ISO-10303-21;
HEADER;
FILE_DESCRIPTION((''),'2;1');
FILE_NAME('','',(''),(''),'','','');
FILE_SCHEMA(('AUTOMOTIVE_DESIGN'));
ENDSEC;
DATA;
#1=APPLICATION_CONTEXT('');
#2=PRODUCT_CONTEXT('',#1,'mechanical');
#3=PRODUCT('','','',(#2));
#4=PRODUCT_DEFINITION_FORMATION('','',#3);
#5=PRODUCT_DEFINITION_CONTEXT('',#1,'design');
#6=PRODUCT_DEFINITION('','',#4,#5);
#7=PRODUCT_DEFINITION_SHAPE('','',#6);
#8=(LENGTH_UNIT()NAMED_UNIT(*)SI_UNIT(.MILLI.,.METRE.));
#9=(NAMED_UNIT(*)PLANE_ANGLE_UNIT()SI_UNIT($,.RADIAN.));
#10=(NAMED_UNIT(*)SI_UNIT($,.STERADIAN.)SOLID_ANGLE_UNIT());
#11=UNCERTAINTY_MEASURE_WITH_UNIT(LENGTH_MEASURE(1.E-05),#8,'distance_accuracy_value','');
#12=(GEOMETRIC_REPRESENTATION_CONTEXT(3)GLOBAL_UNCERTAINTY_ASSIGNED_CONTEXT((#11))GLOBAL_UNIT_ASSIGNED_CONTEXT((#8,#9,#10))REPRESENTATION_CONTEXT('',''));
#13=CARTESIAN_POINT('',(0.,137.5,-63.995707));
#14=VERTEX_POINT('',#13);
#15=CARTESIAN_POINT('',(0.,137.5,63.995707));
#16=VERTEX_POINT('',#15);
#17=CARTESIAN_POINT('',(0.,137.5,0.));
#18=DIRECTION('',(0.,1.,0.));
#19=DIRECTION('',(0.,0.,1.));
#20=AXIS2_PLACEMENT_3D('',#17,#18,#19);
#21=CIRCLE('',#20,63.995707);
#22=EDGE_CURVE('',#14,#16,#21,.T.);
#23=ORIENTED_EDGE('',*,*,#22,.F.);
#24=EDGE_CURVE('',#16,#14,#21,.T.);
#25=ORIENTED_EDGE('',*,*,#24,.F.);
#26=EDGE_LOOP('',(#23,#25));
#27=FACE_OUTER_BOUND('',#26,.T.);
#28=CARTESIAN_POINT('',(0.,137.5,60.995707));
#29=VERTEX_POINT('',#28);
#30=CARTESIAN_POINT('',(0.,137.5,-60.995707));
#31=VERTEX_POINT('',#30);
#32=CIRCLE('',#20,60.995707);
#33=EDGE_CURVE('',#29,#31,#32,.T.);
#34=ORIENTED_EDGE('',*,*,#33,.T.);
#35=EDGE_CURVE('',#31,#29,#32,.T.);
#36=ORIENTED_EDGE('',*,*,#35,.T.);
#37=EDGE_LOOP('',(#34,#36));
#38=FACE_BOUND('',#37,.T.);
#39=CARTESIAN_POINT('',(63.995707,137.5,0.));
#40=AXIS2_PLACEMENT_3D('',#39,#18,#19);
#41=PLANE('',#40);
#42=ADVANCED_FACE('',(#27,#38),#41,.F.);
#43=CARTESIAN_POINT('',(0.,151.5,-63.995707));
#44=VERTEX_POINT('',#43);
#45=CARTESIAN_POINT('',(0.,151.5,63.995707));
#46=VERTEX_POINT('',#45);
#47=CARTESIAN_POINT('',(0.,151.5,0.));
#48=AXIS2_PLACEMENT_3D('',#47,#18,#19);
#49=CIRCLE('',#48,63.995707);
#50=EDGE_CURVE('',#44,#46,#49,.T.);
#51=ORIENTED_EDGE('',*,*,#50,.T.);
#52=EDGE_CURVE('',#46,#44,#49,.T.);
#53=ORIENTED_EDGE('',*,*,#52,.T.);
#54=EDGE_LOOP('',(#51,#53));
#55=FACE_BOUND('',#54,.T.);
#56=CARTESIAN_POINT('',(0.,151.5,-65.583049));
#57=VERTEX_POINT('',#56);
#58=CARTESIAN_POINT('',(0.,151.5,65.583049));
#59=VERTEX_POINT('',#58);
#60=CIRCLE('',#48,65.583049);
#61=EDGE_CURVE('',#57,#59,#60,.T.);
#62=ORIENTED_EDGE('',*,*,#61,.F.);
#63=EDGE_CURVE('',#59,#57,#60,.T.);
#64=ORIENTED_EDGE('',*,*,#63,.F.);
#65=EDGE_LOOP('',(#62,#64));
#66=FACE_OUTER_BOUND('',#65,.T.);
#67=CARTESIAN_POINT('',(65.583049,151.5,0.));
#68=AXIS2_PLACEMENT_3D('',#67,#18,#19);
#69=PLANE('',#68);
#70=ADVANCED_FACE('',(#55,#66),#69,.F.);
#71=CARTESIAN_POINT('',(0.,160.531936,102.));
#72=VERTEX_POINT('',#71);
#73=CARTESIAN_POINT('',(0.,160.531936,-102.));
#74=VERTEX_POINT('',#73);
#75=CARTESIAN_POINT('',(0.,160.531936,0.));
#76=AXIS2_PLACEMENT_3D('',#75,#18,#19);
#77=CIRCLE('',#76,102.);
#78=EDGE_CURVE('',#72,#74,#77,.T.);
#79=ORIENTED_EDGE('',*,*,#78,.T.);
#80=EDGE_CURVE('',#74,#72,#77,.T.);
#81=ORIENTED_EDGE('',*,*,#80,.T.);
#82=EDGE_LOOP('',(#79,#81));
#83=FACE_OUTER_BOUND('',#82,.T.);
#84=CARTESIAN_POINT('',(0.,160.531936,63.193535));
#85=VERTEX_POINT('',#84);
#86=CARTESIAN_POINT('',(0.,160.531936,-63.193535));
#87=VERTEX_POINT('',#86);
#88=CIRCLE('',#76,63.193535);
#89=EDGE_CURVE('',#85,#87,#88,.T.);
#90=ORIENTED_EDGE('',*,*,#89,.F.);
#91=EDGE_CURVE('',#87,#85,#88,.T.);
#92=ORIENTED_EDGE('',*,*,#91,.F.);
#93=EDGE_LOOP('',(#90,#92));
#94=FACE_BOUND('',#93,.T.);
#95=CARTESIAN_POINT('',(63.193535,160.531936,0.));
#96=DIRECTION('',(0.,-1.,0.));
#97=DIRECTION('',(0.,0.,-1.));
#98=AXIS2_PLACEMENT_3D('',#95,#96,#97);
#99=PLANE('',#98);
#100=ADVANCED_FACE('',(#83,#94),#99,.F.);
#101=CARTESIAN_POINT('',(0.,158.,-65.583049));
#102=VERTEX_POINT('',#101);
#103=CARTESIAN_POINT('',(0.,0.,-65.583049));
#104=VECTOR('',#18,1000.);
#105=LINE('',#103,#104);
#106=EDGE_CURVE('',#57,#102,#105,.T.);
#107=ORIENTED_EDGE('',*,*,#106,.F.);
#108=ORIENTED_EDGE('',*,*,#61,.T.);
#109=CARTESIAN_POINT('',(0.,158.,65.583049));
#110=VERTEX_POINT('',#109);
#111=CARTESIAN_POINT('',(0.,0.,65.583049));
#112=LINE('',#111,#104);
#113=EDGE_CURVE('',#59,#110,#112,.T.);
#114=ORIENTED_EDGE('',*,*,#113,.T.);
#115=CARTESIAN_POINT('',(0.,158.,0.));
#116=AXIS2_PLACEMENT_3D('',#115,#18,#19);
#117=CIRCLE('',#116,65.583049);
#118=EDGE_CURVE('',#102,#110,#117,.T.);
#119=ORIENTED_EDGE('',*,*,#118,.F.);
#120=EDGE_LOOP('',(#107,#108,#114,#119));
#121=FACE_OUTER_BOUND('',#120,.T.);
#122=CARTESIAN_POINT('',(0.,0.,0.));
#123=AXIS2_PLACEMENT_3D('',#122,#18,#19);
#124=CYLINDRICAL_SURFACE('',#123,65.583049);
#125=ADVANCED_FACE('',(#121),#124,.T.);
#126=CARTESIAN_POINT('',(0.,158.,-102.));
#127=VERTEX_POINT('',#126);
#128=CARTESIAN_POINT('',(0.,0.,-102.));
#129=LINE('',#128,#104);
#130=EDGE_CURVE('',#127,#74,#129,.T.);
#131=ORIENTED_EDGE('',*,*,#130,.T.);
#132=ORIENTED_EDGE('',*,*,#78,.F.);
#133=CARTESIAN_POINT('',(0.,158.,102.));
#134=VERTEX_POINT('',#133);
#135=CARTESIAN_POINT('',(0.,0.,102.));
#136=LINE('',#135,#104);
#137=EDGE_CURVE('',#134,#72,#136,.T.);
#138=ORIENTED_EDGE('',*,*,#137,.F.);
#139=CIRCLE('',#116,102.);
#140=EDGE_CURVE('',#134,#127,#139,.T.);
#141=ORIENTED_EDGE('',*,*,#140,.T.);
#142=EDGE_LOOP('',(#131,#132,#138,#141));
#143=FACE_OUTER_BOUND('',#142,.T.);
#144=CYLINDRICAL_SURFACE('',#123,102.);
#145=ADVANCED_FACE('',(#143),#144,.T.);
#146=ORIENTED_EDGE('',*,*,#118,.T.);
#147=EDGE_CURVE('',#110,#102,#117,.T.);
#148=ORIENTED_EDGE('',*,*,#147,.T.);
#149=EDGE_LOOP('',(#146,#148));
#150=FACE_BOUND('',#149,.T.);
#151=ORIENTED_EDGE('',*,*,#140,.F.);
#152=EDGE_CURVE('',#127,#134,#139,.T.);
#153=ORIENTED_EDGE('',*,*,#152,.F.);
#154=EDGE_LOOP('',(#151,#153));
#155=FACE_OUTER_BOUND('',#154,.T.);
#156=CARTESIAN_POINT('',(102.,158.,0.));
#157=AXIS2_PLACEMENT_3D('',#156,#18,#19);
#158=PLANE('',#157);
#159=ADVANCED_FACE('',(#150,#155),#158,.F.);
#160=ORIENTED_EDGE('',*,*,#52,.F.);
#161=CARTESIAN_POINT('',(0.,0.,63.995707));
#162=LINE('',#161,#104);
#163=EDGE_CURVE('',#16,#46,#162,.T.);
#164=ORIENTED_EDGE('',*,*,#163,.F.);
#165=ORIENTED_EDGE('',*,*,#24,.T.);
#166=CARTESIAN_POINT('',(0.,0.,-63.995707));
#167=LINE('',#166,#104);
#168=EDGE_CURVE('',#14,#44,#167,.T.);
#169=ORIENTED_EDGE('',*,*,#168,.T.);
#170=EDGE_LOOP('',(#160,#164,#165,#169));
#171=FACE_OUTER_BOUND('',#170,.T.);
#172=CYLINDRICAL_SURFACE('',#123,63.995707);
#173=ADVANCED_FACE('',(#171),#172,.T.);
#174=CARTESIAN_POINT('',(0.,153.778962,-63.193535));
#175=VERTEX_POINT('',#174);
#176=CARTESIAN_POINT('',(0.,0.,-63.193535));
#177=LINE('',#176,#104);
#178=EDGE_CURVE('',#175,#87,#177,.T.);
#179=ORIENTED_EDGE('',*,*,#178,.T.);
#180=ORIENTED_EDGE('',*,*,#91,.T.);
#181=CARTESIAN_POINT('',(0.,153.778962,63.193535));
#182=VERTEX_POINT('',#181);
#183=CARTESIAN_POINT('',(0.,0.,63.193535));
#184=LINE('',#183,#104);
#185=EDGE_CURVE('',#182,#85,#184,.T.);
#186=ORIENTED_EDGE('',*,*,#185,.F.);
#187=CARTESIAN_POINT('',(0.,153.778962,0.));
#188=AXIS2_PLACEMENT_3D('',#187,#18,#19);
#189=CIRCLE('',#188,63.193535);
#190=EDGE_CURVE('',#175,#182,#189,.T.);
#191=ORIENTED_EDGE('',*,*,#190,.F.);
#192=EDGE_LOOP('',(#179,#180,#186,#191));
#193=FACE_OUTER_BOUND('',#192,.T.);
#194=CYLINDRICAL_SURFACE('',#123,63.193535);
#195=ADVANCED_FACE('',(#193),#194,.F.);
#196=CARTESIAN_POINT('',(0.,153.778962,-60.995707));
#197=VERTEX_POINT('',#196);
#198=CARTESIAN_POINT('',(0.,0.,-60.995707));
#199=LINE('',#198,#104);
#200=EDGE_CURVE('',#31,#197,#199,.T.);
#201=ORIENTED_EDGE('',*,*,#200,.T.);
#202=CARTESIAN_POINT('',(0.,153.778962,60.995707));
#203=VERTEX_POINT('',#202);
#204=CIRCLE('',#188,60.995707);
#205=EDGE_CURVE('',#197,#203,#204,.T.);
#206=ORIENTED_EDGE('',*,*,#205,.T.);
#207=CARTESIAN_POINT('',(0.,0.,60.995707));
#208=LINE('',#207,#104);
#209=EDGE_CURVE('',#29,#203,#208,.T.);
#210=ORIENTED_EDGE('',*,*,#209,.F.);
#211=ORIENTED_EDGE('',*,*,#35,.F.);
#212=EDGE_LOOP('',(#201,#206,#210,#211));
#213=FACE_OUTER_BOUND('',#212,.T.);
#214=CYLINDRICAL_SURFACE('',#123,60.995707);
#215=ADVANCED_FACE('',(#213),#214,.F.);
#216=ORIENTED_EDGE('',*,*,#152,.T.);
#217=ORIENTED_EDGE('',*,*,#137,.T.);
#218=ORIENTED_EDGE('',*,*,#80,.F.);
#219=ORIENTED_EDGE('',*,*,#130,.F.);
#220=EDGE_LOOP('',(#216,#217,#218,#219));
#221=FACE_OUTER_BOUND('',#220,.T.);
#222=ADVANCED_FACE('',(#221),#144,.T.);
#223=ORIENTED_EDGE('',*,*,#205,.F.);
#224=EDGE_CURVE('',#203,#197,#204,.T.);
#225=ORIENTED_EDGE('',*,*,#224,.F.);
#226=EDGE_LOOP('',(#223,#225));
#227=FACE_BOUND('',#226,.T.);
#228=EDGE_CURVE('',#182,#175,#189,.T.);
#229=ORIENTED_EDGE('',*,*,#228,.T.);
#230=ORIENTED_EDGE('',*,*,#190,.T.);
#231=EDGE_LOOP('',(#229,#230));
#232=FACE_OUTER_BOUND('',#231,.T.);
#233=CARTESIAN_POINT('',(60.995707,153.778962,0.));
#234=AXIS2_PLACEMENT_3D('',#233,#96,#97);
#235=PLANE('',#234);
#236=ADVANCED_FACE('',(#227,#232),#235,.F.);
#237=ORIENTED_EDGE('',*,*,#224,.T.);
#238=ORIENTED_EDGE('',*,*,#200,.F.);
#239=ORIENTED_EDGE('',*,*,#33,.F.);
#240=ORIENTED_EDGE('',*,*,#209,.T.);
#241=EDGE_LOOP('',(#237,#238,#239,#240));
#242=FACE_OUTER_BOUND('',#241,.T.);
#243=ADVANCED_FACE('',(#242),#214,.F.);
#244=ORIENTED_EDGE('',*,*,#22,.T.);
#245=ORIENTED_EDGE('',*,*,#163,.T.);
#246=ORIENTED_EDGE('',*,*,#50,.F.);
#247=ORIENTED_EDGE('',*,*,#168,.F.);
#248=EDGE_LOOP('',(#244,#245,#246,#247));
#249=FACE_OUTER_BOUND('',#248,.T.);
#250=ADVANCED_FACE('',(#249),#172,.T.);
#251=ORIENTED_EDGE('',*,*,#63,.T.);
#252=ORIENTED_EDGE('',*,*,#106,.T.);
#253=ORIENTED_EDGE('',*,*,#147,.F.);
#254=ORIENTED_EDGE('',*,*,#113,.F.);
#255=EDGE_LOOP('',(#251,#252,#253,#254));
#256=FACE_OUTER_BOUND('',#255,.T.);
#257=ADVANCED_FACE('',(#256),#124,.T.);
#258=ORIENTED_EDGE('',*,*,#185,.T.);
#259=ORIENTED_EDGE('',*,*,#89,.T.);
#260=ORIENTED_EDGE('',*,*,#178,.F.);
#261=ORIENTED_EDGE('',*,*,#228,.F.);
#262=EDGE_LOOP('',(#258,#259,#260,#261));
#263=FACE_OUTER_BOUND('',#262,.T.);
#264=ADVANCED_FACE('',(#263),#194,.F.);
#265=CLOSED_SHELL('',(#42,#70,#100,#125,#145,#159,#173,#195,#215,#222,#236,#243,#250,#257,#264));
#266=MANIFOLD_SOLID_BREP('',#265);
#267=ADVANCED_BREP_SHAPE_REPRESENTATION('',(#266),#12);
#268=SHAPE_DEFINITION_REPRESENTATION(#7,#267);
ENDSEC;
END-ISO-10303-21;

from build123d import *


with BuildPart() as part:
    # Sketch1 → Revolve1 (revolve)
    with BuildSketch(Plane.XY, mode=Mode.PRIVATE) as revolve1_sk:
        Polygon((102, 158), (65.583048881, 158), (65.583048881, 151.5), (63.995706961, 151.5), (63.995706961, 137.5), (60.995706961, 137.5), (60.995706961, 153.778962031), (63.193534924, 153.778962031), (63.193534924, 160.531936258), (102, 160.531936258), align=None)
    revolve(revolve1_sk.sketch.rotate(Axis((0, 0, 0), (0, -1, 0)), 90), axis=Axis((0, 0, 0), (0, -1, 0)))


solid = part.part
